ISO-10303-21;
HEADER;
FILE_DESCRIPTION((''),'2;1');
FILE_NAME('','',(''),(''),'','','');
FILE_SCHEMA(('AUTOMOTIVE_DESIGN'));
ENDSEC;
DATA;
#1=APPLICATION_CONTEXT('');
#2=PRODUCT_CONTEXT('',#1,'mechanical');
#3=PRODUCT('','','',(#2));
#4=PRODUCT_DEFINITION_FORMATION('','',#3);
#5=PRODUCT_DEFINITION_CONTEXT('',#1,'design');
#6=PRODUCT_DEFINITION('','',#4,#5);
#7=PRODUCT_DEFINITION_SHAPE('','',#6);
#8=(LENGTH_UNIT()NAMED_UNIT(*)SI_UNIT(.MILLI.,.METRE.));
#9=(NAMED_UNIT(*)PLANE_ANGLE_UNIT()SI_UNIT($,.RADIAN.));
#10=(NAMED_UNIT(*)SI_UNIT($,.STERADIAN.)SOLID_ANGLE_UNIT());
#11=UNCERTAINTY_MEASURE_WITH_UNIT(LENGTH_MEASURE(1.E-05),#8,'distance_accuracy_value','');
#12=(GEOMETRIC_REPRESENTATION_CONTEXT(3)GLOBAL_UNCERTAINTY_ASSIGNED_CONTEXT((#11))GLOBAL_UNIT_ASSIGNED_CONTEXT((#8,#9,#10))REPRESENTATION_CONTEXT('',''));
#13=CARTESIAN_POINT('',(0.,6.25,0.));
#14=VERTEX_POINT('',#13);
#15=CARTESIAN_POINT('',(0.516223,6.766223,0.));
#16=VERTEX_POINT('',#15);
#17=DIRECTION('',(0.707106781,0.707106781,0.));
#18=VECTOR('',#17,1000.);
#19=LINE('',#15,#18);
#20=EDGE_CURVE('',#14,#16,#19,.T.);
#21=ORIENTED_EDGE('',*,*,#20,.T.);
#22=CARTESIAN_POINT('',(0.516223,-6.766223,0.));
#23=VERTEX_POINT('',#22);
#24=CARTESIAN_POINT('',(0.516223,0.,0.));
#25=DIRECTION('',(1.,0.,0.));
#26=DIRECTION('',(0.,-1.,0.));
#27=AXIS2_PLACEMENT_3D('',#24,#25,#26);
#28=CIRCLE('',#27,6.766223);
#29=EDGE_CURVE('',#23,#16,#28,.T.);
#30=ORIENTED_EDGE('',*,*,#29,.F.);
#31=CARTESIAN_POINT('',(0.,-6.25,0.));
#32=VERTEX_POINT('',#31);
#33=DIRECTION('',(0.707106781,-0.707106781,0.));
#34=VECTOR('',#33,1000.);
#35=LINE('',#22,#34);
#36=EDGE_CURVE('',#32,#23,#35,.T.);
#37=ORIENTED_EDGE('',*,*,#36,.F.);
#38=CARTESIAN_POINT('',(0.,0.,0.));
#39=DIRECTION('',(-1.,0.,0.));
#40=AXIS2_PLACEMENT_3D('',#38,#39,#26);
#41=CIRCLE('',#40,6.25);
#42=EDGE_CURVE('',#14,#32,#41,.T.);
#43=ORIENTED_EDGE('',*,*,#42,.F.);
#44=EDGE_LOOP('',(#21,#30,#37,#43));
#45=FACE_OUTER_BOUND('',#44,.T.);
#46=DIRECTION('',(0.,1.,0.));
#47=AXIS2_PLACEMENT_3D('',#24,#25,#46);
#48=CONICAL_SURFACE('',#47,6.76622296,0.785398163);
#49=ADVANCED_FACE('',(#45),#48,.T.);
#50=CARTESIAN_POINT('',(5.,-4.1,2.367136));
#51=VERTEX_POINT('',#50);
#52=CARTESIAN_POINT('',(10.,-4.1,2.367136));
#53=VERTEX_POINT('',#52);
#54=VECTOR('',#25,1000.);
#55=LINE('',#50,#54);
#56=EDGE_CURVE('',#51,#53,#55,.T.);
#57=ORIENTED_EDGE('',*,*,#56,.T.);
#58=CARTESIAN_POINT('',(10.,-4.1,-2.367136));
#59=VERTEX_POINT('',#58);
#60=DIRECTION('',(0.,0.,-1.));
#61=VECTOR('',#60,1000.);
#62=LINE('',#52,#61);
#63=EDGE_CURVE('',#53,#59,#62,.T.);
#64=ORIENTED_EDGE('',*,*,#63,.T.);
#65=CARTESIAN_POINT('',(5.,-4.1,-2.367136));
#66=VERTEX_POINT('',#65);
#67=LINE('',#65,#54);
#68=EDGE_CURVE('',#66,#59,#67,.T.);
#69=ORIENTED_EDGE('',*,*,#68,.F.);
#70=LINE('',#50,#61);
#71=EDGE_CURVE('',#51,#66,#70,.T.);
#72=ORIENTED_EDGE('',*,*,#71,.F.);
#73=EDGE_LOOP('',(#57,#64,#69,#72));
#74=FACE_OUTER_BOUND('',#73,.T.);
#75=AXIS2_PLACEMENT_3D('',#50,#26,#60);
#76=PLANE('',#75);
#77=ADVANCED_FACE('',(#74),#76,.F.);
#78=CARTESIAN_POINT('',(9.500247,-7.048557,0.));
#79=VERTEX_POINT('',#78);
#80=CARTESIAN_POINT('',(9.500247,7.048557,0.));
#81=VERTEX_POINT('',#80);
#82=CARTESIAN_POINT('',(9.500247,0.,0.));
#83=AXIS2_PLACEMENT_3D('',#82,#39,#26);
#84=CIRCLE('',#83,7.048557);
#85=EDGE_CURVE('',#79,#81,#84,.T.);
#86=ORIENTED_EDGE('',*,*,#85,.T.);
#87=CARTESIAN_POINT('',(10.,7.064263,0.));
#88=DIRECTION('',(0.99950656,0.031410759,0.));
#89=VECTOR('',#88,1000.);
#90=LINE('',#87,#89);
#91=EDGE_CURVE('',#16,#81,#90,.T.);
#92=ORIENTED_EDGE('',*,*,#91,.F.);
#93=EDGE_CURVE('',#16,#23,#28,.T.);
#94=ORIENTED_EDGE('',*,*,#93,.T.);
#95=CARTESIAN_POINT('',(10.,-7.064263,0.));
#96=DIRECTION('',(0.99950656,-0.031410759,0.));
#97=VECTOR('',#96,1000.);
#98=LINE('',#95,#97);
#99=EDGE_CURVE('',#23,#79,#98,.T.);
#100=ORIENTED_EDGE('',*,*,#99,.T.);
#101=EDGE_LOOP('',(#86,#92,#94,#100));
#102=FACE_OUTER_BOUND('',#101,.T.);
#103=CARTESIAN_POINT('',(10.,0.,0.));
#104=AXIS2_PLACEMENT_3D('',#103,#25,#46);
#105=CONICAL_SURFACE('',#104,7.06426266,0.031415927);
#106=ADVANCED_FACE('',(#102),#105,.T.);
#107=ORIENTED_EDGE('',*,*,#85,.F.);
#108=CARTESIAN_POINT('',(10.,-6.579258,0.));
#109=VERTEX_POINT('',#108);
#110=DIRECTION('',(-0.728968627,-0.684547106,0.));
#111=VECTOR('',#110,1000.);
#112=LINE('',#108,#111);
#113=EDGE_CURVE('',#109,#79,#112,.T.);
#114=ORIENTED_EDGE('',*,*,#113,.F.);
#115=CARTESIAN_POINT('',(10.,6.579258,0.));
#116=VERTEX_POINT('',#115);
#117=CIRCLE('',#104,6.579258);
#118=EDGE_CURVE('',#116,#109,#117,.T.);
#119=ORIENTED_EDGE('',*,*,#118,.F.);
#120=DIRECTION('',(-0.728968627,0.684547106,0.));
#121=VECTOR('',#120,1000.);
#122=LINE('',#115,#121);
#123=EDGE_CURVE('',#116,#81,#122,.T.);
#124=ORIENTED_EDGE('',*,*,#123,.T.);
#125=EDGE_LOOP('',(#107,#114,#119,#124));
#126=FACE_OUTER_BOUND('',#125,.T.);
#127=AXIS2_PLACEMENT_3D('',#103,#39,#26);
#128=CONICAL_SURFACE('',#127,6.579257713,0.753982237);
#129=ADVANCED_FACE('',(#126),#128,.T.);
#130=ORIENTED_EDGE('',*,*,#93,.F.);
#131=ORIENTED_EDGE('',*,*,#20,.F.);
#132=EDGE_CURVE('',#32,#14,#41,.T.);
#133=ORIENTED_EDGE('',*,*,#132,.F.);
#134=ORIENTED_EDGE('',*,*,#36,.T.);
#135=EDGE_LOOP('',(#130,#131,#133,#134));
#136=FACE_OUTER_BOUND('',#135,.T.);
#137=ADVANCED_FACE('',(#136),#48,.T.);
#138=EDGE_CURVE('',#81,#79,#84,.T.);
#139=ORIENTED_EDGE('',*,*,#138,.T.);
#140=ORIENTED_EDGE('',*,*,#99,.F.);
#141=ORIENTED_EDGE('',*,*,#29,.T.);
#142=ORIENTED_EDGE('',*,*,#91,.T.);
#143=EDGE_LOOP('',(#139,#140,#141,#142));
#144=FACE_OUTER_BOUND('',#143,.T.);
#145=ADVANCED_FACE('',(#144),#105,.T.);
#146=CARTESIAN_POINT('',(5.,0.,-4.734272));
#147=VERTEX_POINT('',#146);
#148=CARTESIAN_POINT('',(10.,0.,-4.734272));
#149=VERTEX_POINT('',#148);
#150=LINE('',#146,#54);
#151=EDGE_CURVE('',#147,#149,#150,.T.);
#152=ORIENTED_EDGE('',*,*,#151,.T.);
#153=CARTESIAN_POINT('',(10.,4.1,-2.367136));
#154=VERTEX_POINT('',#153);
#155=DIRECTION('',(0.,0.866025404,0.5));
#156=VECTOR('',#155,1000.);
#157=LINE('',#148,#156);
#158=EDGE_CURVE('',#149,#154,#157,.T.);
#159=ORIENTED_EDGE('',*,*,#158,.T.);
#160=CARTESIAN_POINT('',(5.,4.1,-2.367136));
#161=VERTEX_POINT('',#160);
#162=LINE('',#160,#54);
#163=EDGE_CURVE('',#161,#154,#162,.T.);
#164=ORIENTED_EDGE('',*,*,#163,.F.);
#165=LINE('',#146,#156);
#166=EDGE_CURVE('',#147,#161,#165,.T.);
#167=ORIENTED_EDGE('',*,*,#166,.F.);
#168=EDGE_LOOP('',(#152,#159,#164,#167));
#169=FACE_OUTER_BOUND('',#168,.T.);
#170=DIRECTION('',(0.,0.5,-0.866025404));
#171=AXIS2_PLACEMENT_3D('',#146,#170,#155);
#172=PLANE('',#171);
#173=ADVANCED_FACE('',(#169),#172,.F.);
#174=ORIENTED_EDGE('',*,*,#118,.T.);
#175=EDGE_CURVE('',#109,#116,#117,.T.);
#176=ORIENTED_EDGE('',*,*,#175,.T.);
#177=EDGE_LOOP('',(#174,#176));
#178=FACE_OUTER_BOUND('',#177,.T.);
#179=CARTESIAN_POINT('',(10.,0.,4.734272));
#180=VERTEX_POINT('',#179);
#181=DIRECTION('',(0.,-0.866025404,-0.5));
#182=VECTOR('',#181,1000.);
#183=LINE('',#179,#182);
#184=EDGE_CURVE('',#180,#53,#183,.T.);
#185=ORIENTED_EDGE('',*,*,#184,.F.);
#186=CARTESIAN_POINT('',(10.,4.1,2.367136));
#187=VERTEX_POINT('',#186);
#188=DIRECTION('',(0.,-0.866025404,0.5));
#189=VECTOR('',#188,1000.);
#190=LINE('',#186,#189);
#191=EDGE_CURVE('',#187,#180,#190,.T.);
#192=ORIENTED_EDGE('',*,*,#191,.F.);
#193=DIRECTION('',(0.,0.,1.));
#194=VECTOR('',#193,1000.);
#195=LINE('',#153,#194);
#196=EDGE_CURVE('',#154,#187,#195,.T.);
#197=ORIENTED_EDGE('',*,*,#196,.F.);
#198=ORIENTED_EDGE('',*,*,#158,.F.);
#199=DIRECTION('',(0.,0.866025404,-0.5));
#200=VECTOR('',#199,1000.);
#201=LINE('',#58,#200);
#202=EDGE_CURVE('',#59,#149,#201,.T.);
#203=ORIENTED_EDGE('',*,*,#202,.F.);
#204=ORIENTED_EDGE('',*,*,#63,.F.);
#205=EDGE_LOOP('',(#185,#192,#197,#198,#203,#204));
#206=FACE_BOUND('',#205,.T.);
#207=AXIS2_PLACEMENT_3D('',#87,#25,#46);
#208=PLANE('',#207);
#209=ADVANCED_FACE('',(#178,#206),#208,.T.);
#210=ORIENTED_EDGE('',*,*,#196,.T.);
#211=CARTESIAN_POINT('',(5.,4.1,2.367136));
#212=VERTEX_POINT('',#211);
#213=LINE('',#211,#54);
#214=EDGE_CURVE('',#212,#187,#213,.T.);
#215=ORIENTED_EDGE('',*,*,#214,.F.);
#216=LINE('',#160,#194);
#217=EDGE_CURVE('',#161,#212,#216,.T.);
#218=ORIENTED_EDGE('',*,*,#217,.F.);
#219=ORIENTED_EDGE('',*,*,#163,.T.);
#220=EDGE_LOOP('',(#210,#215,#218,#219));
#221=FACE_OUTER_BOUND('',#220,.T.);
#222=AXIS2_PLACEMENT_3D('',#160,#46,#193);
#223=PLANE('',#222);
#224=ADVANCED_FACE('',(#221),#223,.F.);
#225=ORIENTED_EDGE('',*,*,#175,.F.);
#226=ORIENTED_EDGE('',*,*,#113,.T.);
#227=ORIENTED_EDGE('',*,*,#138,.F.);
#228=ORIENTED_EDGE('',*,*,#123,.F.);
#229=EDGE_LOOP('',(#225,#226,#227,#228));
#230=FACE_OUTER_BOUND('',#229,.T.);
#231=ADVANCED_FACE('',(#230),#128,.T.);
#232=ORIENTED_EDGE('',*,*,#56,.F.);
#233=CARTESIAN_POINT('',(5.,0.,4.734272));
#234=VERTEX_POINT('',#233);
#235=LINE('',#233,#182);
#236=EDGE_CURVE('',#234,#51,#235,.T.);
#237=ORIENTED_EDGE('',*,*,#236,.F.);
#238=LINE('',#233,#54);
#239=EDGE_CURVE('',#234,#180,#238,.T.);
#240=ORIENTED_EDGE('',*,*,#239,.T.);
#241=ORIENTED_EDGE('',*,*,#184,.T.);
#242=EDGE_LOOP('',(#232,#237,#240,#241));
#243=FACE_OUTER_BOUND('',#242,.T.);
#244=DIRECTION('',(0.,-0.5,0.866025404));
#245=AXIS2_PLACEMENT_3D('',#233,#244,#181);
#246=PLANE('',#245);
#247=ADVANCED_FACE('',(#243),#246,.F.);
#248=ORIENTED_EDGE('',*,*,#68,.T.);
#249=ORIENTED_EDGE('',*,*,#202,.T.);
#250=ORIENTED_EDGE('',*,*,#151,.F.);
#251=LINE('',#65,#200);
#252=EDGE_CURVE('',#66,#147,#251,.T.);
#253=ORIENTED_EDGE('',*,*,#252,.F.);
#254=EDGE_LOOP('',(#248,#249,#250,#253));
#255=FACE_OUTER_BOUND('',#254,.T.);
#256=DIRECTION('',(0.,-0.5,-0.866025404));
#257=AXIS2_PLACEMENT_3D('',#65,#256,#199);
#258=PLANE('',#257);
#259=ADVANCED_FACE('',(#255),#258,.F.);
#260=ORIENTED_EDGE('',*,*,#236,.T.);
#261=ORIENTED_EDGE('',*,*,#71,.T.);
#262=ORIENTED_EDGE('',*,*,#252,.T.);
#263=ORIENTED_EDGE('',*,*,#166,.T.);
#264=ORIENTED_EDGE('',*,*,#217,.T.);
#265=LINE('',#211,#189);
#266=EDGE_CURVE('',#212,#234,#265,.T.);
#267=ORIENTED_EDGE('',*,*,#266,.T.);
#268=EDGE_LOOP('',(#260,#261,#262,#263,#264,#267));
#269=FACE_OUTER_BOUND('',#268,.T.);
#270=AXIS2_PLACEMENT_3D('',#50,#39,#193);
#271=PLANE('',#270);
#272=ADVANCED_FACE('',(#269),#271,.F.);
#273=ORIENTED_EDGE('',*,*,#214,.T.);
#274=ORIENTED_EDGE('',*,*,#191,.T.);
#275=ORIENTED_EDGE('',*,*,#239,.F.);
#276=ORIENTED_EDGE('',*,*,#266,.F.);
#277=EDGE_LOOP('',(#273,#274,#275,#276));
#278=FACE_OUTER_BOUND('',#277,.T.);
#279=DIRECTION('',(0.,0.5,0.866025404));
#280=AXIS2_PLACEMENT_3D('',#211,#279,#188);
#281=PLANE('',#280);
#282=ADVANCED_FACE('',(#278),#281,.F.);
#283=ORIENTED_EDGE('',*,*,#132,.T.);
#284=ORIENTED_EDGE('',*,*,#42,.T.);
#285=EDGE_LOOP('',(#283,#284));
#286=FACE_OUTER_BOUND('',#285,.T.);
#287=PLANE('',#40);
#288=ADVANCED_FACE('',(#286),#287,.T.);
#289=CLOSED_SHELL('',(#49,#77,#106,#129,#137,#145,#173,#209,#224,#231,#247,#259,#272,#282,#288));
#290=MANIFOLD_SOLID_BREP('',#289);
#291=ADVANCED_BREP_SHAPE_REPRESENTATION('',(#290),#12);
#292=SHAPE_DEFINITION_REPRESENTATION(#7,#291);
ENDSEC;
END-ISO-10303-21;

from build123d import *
from OCP.BRepFilletAPI import BRepFilletAPI_MakeChamfer

# Parameters (mm, degrees)
CUT_EXTRUDE_1_DEPTH = 5
CHAMFER_1_SIZE      = 0.5
CHAMFER_1_SIZE2     = 0.516477811
CHAMFER_1_SIZE2_2   = 0.485004947


with BuildPart() as part:
    # 草图1 → 旋转1 (revolve)
    with BuildSketch(Plane.XY):
        Polygon((0, 0), (0, 6.75), (10, 7.06426266), (10, 0), align=None)
    revolve(axis=Axis((0, 0, 0), (-1, 0, 0)))

    # 草图2 → 切除-拉伸1 (cut)
    with BuildSketch(Plane(origin=(10, 0, 0), x_dir=(0, 0, -1), z_dir=(1, 0, 0))):
        Polygon((2.367136104, -4.1), (4.734272207, 0), (2.367136104, 4.1), (-2.367136104, 4.1), (-4.734272207, 0), (-2.367136104, -4.1), align=None)
    extrude(amount=-CUT_EXTRUDE_1_DEPTH, mode=Mode.SUBTRACT)

    # 倒角1: one chamfer whose edges measure the first distance from different faces: ONE call of the kernel's chamfer builder (chamfer() names one face for all edges)
    chamfer_1_edges_1 = [part.edges().sort_by_distance(p)[0] for p in [
        (0, -6.75, 0),
    ]]
    chamfer_1_side_1 = [part.faces().sort_by_distance(p)[0] for p in [
        (0, 0, 0),
    ]]
    chamfer_1_edges_2 = [part.edges().sort_by_distance(p)[0] for p in [
        (10, -7.06426266, 0),
    ]]
    chamfer_1_side_2 = [part.faces().sort_by_distance(p)[0] for p in [
        (5, -6.90713133, 0),
    ]]
    chamfer_1 = BRepFilletAPI_MakeChamfer(part.part.solid().wrapped)
    for e in chamfer_1_edges_1:
        chamfer_1.Add(CHAMFER_1_SIZE, CHAMFER_1_SIZE2, e.wrapped, chamfer_1_side_1[0].wrapped)  # the first distance lies on this face
    for e in chamfer_1_edges_2:
        chamfer_1.Add(CHAMFER_1_SIZE, CHAMFER_1_SIZE2_2, e.wrapped, chamfer_1_side_2[0].wrapped)  # the first distance lies on this face
    add(Compound.cast(chamfer_1.Shape()), mode=Mode.REPLACE)


solid = part.part
